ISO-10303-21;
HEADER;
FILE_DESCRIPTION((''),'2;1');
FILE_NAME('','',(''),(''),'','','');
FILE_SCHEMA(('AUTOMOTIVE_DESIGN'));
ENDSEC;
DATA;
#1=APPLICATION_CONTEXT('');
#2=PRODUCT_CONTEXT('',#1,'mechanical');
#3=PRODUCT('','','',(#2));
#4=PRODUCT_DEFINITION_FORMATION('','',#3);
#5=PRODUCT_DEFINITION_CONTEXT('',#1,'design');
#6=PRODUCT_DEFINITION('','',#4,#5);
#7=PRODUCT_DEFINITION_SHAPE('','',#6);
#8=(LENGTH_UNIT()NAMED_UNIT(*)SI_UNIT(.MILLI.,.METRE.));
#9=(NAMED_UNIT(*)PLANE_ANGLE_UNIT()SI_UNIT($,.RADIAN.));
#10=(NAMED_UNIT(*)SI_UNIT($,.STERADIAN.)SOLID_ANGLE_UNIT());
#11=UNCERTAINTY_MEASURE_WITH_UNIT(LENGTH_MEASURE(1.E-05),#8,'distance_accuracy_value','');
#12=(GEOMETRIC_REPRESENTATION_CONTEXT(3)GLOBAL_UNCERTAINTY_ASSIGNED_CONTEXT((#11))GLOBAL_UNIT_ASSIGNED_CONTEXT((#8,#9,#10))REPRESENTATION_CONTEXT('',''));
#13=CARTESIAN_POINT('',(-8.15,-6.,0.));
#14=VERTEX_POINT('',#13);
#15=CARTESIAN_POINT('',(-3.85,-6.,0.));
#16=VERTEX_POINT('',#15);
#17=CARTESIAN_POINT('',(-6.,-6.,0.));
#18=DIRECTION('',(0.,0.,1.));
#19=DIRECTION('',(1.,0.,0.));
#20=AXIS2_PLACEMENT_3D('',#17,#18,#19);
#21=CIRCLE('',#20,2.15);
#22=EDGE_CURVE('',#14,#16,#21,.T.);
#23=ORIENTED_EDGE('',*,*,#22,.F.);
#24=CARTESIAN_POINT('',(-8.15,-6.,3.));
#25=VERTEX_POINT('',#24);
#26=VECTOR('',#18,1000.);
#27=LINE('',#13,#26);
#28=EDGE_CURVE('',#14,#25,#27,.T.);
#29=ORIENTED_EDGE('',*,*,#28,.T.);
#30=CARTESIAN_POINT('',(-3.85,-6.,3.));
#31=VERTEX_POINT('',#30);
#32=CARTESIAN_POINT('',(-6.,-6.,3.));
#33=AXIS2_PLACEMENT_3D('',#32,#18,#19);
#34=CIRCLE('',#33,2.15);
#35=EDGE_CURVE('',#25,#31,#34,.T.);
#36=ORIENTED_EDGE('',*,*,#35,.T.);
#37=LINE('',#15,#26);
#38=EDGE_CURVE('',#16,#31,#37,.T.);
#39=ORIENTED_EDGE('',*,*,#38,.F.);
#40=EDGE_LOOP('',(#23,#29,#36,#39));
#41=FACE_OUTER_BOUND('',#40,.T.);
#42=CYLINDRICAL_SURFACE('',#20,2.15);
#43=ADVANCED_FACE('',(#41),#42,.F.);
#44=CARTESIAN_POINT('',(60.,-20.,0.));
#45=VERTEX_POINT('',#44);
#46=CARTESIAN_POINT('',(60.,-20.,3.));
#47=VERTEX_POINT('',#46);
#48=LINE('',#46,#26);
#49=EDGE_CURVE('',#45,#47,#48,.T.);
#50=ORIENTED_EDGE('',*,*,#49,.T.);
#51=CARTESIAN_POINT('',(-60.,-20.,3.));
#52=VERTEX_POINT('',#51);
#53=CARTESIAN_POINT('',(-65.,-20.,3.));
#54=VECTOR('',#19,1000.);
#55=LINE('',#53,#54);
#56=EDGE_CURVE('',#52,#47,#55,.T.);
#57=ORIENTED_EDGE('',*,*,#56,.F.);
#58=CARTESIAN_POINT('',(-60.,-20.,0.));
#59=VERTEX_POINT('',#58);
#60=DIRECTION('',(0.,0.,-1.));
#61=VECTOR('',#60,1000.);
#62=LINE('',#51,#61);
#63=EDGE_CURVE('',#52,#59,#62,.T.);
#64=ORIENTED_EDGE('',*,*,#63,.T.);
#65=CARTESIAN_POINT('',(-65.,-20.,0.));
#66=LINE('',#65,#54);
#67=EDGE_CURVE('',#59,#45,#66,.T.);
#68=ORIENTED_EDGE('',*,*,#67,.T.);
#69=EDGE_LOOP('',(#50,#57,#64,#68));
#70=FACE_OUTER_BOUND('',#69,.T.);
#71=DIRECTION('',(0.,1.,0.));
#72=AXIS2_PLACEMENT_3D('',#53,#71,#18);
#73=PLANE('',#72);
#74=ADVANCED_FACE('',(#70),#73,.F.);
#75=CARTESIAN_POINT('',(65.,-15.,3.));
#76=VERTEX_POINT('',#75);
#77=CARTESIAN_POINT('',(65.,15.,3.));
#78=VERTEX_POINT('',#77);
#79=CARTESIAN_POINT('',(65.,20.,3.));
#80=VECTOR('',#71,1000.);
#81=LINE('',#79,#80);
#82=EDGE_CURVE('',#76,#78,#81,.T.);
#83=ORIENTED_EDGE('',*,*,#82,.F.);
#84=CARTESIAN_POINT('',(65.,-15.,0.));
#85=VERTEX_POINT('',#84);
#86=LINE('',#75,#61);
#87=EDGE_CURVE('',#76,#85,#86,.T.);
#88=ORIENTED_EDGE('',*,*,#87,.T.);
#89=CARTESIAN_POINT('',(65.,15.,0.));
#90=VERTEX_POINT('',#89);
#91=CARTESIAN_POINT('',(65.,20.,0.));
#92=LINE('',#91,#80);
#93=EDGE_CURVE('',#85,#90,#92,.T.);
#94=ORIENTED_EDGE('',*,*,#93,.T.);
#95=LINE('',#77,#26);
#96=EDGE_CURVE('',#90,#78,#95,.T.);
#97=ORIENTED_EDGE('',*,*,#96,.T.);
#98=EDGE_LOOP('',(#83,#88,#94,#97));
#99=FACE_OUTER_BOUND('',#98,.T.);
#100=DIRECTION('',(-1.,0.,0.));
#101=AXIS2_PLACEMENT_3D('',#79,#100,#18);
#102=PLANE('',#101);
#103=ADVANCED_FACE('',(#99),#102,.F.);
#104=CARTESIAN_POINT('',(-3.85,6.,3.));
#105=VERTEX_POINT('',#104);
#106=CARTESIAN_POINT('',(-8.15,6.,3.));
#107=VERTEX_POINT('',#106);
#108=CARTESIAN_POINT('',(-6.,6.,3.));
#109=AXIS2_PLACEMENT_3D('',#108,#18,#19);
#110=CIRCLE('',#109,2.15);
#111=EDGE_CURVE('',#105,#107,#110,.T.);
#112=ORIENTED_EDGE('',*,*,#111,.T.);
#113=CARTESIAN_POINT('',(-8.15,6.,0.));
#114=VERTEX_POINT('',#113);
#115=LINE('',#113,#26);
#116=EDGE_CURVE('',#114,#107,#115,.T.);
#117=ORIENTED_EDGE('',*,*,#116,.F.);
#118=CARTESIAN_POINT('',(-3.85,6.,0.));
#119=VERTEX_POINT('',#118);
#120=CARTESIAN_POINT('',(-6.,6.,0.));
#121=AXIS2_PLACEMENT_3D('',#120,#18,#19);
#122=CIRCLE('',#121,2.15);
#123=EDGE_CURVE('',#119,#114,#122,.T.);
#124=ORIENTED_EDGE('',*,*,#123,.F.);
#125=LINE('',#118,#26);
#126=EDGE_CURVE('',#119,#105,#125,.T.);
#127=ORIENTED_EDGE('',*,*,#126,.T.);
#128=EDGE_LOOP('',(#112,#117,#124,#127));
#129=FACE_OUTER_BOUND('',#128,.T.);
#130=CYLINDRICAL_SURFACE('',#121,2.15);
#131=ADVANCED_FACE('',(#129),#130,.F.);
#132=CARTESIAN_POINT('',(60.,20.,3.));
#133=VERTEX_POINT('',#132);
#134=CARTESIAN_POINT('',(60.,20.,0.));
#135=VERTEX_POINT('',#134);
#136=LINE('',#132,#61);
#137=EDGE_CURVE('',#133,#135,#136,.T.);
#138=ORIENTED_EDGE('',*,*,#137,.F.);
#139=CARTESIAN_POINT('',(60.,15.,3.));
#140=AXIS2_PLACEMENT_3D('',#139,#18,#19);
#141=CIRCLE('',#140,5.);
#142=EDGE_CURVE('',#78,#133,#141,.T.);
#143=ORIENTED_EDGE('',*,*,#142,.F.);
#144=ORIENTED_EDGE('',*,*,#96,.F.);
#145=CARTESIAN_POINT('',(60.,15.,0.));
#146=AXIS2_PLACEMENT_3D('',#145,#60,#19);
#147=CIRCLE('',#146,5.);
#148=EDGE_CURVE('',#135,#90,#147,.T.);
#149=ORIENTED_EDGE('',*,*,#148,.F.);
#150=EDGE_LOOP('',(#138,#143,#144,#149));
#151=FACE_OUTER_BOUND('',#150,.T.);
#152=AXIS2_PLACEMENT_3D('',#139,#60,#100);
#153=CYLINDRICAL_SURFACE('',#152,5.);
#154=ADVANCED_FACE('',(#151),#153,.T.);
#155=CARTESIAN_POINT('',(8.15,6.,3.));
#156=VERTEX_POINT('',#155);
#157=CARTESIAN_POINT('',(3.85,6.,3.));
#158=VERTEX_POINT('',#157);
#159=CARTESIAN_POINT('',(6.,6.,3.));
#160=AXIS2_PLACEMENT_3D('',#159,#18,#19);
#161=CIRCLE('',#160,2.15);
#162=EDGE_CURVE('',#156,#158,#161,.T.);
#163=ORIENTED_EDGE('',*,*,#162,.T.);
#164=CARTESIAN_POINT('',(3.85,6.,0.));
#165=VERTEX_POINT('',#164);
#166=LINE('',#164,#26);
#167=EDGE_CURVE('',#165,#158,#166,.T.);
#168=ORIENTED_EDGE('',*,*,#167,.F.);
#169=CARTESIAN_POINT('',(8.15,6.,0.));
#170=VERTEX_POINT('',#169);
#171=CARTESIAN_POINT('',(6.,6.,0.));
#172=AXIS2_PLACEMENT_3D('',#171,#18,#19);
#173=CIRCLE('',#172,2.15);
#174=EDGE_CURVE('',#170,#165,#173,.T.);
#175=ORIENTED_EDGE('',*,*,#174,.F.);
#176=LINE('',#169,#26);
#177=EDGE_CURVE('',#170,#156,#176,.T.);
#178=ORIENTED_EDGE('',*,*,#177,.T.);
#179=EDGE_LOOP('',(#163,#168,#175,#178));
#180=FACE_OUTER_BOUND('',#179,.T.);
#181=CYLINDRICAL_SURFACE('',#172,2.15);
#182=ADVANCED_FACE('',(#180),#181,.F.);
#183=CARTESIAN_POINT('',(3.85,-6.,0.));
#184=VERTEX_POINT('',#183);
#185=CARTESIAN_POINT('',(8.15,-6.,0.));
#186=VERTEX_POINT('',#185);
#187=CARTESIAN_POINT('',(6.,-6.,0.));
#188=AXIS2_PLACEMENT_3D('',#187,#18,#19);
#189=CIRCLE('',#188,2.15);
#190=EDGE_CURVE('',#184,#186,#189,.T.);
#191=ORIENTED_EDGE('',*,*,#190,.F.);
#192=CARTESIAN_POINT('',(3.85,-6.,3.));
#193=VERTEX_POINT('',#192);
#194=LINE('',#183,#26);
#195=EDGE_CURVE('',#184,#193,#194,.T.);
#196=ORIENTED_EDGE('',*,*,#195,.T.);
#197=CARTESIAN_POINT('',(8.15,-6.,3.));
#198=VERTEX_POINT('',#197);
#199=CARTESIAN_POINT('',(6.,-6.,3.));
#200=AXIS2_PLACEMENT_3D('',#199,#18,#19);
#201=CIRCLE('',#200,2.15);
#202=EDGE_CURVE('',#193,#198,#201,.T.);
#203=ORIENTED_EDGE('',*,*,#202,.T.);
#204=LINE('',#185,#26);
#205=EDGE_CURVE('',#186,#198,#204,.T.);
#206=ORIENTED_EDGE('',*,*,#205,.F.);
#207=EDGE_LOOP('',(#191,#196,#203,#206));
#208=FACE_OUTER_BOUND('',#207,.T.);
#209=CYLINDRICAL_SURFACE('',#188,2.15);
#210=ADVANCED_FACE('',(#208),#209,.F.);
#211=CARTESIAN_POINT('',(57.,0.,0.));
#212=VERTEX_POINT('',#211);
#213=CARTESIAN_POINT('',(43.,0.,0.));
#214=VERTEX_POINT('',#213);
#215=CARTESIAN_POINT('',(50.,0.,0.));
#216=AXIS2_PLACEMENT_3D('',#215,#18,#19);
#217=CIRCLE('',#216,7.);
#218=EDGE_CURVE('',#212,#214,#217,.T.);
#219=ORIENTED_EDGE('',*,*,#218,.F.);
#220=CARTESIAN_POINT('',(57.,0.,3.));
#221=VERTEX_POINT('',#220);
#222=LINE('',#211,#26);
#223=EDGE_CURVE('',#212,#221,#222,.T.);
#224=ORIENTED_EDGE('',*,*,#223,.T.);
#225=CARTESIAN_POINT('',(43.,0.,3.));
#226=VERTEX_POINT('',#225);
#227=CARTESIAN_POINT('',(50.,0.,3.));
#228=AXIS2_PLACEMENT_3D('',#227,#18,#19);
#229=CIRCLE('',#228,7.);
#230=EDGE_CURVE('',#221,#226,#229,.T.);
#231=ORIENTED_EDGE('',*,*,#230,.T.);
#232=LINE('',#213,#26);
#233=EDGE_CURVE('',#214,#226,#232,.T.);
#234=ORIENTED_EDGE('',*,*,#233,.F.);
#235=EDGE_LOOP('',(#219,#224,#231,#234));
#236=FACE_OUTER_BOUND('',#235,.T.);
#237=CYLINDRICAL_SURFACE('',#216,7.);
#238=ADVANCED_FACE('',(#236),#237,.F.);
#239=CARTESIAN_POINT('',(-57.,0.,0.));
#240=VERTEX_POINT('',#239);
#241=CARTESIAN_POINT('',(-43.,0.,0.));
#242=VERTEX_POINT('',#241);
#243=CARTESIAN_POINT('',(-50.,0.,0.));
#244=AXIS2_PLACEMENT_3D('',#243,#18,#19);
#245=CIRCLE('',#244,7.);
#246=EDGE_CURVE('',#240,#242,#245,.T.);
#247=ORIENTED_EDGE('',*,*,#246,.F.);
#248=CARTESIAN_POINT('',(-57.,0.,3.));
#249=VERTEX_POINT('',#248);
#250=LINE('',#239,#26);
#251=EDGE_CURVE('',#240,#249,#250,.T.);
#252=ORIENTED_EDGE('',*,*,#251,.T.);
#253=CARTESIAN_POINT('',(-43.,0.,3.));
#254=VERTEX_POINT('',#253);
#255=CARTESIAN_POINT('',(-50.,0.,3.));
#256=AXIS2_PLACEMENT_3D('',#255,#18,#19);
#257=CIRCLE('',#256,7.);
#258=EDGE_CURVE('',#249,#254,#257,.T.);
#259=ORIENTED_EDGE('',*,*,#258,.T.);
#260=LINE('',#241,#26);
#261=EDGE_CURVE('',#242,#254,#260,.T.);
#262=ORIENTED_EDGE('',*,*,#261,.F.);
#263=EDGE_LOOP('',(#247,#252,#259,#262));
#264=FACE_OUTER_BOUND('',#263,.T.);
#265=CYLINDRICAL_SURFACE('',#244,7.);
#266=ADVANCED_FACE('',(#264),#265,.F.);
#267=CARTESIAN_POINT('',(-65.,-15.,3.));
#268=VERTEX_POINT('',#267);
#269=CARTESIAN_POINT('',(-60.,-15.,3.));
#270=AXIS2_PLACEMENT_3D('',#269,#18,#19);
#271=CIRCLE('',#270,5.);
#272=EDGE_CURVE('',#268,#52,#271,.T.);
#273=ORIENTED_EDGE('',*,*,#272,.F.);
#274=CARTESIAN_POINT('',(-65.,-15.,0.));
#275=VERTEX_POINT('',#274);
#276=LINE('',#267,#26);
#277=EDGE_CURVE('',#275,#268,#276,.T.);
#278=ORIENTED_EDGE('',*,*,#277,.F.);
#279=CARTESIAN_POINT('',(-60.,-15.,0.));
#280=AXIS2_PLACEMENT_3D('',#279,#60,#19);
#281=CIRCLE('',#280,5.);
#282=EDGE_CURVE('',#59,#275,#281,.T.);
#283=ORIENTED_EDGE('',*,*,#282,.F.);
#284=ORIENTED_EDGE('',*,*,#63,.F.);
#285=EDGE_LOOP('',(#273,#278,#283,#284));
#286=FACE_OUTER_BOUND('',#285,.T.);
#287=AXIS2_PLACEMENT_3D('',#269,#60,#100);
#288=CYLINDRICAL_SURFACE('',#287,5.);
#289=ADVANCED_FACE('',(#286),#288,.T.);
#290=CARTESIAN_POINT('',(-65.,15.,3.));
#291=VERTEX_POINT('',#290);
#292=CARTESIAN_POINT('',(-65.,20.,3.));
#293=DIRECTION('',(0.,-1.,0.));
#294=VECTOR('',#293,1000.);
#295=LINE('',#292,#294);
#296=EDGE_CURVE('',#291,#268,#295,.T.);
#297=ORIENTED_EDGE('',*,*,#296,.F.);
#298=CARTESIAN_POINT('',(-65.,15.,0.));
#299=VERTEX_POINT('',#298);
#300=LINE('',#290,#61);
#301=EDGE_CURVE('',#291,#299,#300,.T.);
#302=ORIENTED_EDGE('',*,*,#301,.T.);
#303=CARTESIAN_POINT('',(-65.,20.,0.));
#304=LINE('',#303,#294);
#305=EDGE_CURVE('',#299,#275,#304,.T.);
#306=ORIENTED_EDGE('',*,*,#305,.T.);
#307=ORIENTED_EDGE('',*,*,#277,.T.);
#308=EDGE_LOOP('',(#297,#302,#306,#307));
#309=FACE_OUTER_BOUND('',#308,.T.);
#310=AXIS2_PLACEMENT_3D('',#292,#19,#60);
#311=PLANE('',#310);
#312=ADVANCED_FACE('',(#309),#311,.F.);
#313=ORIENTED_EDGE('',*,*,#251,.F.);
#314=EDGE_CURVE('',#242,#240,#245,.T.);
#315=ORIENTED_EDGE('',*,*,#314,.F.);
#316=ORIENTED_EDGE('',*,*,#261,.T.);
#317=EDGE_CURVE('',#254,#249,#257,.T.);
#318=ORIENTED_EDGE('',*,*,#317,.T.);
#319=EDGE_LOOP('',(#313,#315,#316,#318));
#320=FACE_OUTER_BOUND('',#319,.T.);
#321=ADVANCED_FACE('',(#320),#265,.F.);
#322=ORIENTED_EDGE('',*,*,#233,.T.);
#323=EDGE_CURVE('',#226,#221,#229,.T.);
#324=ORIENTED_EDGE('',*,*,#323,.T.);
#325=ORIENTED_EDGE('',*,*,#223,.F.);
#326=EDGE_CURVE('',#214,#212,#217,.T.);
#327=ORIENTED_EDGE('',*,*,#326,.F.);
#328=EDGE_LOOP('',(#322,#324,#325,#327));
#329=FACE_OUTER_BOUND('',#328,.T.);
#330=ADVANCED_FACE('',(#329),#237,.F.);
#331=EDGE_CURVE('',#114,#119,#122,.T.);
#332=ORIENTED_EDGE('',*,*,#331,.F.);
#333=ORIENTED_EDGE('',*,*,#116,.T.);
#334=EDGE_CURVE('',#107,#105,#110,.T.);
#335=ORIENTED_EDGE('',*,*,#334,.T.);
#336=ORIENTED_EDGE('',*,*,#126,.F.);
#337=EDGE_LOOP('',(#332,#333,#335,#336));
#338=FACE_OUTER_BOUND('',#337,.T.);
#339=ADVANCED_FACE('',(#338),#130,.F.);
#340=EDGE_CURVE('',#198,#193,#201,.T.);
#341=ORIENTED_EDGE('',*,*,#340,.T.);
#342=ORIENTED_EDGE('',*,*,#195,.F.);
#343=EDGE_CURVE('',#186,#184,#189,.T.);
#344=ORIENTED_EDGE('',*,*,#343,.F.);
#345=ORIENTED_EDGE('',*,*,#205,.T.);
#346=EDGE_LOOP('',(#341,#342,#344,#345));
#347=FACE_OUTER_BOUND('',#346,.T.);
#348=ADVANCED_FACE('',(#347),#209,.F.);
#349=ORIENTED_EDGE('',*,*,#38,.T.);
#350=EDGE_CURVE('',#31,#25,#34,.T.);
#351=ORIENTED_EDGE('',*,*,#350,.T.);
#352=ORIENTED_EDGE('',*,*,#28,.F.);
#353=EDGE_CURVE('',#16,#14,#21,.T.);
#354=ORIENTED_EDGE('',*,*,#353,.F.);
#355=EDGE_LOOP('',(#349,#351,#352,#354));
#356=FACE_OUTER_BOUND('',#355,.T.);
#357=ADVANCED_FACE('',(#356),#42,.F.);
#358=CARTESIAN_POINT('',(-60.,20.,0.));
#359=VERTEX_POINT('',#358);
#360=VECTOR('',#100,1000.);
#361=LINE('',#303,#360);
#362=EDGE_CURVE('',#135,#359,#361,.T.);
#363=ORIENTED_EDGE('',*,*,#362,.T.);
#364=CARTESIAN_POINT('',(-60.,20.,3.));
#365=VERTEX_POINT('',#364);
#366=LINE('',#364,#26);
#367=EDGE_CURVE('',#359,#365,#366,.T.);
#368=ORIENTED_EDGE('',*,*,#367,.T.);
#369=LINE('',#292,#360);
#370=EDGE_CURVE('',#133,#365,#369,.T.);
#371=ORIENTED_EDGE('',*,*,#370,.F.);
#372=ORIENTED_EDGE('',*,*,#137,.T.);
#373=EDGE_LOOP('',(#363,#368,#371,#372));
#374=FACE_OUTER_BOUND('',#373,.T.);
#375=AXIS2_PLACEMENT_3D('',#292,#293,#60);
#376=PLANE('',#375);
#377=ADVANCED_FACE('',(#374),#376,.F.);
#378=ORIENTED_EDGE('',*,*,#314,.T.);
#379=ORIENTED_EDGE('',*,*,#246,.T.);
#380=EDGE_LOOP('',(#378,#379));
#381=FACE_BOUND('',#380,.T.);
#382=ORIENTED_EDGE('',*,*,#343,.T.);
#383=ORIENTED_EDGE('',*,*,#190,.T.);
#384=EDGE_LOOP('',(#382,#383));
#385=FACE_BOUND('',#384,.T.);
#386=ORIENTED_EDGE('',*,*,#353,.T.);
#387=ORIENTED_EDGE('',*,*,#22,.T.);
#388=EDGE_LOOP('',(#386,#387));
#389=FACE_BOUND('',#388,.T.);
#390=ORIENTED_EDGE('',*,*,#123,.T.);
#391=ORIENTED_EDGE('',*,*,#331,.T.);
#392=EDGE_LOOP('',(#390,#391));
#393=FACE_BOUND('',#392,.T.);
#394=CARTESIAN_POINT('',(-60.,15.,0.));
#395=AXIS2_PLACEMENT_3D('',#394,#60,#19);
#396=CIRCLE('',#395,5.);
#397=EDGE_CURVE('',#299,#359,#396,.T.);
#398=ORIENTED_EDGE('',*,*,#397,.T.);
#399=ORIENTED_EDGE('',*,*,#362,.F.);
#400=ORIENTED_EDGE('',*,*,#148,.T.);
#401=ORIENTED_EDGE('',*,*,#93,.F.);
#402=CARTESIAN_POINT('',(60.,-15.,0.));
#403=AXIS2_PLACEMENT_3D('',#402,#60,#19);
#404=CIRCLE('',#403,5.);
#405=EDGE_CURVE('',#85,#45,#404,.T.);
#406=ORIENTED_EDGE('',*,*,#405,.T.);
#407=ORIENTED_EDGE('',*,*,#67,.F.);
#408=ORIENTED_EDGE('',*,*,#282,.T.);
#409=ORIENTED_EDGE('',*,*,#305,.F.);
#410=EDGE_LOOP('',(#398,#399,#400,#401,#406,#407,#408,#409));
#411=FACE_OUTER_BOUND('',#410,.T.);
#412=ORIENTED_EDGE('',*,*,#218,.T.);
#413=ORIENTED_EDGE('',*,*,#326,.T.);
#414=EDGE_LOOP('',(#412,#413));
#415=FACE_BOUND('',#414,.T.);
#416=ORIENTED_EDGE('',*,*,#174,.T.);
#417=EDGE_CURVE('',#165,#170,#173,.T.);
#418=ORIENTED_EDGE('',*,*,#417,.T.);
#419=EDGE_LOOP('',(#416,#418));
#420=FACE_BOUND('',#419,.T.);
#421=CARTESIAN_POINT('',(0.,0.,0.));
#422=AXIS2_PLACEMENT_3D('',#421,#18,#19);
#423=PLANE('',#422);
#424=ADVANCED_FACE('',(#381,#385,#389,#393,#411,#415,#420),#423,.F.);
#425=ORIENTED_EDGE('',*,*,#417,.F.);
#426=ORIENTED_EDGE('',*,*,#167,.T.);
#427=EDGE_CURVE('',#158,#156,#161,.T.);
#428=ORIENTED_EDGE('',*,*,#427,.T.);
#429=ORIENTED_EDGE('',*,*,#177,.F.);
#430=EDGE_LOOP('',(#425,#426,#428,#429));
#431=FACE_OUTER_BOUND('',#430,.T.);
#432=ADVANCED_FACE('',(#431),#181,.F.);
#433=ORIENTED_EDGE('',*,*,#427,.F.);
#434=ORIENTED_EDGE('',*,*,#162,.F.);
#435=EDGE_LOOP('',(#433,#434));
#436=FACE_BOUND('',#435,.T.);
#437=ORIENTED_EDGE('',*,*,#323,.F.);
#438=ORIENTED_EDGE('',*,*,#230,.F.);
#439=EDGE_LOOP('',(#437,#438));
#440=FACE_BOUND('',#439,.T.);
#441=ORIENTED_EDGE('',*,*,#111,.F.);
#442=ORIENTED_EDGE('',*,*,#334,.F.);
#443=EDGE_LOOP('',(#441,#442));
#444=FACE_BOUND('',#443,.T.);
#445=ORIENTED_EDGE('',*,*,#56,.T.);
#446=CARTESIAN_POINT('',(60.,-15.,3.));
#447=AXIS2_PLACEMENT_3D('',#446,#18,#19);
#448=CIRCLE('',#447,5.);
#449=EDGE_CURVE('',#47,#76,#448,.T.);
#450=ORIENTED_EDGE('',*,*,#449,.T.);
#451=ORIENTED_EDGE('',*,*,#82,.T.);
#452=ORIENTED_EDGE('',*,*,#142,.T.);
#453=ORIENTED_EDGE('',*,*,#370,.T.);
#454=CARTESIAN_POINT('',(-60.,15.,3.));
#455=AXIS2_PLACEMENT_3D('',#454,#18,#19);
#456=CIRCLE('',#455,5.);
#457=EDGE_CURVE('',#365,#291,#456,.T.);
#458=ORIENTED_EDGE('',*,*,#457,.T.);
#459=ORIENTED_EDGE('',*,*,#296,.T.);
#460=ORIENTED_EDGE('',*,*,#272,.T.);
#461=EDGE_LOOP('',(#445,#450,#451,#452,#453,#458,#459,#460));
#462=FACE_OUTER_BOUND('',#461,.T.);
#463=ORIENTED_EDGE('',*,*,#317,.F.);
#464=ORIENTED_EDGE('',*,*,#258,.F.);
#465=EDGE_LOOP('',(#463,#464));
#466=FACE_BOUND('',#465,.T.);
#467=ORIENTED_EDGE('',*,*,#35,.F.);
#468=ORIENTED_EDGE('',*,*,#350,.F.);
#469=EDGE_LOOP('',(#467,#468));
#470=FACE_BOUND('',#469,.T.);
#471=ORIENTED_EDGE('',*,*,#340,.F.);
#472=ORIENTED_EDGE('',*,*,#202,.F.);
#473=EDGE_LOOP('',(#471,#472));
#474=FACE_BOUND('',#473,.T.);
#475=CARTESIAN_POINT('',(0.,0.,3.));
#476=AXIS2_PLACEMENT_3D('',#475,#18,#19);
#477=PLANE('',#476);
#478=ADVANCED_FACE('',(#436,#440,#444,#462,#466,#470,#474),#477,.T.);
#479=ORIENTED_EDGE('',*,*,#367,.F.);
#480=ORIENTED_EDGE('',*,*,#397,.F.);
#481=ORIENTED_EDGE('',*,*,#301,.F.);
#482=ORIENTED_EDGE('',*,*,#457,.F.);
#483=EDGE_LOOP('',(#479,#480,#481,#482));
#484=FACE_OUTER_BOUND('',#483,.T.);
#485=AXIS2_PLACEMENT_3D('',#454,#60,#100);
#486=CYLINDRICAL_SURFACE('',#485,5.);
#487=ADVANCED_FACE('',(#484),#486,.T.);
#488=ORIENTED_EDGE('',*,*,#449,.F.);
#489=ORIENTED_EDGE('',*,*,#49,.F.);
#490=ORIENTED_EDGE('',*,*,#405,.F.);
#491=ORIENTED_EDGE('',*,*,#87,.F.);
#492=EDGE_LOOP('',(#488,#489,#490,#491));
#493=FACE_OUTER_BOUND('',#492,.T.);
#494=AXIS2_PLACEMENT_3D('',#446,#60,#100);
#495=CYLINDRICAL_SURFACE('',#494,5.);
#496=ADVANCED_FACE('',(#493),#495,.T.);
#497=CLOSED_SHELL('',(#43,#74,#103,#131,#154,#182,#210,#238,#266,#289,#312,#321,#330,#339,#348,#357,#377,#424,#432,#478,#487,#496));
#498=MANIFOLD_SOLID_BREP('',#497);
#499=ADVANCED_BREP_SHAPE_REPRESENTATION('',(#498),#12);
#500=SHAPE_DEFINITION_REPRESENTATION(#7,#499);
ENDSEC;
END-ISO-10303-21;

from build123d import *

# Parameters (mm, degrees)
SKETCH_1_W          = 130
SKETCH_1_H          = 40
EXTRUDE_1_DEPTH     = 3
SKETCH_2_R          = 7
SKETCH_2_R_2        = 2.15
CUT_EXTRUDE_1_DEPTH = 3
FILLET_1_R          = 5


with BuildPart() as part:
    # 草图1 → 凸台-拉伸1 (new body)
    with BuildSketch(Plane.XY):
        Rectangle(SKETCH_1_W, SKETCH_1_H)
    extrude(amount=EXTRUDE_1_DEPTH)

    # 草图2 → 切除-拉伸1 (cut)
    with BuildSketch(Plane.XY.offset(3)):
        with Locations((-50, 0)):
            Circle(SKETCH_2_R)
        with Locations((50, 0)):
            Circle(SKETCH_2_R)
        with Locations((-6, 6)):
            Circle(SKETCH_2_R_2)
        with Locations((6, 6)):
            Circle(SKETCH_2_R_2)
        with Locations((6, -6)):
            Circle(SKETCH_2_R_2)
        with Locations((-6, -6)):
            Circle(SKETCH_2_R_2)
    extrude(amount=-CUT_EXTRUDE_1_DEPTH, mode=Mode.SUBTRACT)

    # 圆角1
    fillet_1_edges = [part.edges().sort_by_distance(p)[0] for p in [
        (65, -20, 1.5),
        (-65, -20, 1.5),
        (-65, 20, 1.5),
        (65, 20, 1.5),
    ]]
    fillet(fillet_1_edges, radius=FILLET_1_R)


solid = part.part
